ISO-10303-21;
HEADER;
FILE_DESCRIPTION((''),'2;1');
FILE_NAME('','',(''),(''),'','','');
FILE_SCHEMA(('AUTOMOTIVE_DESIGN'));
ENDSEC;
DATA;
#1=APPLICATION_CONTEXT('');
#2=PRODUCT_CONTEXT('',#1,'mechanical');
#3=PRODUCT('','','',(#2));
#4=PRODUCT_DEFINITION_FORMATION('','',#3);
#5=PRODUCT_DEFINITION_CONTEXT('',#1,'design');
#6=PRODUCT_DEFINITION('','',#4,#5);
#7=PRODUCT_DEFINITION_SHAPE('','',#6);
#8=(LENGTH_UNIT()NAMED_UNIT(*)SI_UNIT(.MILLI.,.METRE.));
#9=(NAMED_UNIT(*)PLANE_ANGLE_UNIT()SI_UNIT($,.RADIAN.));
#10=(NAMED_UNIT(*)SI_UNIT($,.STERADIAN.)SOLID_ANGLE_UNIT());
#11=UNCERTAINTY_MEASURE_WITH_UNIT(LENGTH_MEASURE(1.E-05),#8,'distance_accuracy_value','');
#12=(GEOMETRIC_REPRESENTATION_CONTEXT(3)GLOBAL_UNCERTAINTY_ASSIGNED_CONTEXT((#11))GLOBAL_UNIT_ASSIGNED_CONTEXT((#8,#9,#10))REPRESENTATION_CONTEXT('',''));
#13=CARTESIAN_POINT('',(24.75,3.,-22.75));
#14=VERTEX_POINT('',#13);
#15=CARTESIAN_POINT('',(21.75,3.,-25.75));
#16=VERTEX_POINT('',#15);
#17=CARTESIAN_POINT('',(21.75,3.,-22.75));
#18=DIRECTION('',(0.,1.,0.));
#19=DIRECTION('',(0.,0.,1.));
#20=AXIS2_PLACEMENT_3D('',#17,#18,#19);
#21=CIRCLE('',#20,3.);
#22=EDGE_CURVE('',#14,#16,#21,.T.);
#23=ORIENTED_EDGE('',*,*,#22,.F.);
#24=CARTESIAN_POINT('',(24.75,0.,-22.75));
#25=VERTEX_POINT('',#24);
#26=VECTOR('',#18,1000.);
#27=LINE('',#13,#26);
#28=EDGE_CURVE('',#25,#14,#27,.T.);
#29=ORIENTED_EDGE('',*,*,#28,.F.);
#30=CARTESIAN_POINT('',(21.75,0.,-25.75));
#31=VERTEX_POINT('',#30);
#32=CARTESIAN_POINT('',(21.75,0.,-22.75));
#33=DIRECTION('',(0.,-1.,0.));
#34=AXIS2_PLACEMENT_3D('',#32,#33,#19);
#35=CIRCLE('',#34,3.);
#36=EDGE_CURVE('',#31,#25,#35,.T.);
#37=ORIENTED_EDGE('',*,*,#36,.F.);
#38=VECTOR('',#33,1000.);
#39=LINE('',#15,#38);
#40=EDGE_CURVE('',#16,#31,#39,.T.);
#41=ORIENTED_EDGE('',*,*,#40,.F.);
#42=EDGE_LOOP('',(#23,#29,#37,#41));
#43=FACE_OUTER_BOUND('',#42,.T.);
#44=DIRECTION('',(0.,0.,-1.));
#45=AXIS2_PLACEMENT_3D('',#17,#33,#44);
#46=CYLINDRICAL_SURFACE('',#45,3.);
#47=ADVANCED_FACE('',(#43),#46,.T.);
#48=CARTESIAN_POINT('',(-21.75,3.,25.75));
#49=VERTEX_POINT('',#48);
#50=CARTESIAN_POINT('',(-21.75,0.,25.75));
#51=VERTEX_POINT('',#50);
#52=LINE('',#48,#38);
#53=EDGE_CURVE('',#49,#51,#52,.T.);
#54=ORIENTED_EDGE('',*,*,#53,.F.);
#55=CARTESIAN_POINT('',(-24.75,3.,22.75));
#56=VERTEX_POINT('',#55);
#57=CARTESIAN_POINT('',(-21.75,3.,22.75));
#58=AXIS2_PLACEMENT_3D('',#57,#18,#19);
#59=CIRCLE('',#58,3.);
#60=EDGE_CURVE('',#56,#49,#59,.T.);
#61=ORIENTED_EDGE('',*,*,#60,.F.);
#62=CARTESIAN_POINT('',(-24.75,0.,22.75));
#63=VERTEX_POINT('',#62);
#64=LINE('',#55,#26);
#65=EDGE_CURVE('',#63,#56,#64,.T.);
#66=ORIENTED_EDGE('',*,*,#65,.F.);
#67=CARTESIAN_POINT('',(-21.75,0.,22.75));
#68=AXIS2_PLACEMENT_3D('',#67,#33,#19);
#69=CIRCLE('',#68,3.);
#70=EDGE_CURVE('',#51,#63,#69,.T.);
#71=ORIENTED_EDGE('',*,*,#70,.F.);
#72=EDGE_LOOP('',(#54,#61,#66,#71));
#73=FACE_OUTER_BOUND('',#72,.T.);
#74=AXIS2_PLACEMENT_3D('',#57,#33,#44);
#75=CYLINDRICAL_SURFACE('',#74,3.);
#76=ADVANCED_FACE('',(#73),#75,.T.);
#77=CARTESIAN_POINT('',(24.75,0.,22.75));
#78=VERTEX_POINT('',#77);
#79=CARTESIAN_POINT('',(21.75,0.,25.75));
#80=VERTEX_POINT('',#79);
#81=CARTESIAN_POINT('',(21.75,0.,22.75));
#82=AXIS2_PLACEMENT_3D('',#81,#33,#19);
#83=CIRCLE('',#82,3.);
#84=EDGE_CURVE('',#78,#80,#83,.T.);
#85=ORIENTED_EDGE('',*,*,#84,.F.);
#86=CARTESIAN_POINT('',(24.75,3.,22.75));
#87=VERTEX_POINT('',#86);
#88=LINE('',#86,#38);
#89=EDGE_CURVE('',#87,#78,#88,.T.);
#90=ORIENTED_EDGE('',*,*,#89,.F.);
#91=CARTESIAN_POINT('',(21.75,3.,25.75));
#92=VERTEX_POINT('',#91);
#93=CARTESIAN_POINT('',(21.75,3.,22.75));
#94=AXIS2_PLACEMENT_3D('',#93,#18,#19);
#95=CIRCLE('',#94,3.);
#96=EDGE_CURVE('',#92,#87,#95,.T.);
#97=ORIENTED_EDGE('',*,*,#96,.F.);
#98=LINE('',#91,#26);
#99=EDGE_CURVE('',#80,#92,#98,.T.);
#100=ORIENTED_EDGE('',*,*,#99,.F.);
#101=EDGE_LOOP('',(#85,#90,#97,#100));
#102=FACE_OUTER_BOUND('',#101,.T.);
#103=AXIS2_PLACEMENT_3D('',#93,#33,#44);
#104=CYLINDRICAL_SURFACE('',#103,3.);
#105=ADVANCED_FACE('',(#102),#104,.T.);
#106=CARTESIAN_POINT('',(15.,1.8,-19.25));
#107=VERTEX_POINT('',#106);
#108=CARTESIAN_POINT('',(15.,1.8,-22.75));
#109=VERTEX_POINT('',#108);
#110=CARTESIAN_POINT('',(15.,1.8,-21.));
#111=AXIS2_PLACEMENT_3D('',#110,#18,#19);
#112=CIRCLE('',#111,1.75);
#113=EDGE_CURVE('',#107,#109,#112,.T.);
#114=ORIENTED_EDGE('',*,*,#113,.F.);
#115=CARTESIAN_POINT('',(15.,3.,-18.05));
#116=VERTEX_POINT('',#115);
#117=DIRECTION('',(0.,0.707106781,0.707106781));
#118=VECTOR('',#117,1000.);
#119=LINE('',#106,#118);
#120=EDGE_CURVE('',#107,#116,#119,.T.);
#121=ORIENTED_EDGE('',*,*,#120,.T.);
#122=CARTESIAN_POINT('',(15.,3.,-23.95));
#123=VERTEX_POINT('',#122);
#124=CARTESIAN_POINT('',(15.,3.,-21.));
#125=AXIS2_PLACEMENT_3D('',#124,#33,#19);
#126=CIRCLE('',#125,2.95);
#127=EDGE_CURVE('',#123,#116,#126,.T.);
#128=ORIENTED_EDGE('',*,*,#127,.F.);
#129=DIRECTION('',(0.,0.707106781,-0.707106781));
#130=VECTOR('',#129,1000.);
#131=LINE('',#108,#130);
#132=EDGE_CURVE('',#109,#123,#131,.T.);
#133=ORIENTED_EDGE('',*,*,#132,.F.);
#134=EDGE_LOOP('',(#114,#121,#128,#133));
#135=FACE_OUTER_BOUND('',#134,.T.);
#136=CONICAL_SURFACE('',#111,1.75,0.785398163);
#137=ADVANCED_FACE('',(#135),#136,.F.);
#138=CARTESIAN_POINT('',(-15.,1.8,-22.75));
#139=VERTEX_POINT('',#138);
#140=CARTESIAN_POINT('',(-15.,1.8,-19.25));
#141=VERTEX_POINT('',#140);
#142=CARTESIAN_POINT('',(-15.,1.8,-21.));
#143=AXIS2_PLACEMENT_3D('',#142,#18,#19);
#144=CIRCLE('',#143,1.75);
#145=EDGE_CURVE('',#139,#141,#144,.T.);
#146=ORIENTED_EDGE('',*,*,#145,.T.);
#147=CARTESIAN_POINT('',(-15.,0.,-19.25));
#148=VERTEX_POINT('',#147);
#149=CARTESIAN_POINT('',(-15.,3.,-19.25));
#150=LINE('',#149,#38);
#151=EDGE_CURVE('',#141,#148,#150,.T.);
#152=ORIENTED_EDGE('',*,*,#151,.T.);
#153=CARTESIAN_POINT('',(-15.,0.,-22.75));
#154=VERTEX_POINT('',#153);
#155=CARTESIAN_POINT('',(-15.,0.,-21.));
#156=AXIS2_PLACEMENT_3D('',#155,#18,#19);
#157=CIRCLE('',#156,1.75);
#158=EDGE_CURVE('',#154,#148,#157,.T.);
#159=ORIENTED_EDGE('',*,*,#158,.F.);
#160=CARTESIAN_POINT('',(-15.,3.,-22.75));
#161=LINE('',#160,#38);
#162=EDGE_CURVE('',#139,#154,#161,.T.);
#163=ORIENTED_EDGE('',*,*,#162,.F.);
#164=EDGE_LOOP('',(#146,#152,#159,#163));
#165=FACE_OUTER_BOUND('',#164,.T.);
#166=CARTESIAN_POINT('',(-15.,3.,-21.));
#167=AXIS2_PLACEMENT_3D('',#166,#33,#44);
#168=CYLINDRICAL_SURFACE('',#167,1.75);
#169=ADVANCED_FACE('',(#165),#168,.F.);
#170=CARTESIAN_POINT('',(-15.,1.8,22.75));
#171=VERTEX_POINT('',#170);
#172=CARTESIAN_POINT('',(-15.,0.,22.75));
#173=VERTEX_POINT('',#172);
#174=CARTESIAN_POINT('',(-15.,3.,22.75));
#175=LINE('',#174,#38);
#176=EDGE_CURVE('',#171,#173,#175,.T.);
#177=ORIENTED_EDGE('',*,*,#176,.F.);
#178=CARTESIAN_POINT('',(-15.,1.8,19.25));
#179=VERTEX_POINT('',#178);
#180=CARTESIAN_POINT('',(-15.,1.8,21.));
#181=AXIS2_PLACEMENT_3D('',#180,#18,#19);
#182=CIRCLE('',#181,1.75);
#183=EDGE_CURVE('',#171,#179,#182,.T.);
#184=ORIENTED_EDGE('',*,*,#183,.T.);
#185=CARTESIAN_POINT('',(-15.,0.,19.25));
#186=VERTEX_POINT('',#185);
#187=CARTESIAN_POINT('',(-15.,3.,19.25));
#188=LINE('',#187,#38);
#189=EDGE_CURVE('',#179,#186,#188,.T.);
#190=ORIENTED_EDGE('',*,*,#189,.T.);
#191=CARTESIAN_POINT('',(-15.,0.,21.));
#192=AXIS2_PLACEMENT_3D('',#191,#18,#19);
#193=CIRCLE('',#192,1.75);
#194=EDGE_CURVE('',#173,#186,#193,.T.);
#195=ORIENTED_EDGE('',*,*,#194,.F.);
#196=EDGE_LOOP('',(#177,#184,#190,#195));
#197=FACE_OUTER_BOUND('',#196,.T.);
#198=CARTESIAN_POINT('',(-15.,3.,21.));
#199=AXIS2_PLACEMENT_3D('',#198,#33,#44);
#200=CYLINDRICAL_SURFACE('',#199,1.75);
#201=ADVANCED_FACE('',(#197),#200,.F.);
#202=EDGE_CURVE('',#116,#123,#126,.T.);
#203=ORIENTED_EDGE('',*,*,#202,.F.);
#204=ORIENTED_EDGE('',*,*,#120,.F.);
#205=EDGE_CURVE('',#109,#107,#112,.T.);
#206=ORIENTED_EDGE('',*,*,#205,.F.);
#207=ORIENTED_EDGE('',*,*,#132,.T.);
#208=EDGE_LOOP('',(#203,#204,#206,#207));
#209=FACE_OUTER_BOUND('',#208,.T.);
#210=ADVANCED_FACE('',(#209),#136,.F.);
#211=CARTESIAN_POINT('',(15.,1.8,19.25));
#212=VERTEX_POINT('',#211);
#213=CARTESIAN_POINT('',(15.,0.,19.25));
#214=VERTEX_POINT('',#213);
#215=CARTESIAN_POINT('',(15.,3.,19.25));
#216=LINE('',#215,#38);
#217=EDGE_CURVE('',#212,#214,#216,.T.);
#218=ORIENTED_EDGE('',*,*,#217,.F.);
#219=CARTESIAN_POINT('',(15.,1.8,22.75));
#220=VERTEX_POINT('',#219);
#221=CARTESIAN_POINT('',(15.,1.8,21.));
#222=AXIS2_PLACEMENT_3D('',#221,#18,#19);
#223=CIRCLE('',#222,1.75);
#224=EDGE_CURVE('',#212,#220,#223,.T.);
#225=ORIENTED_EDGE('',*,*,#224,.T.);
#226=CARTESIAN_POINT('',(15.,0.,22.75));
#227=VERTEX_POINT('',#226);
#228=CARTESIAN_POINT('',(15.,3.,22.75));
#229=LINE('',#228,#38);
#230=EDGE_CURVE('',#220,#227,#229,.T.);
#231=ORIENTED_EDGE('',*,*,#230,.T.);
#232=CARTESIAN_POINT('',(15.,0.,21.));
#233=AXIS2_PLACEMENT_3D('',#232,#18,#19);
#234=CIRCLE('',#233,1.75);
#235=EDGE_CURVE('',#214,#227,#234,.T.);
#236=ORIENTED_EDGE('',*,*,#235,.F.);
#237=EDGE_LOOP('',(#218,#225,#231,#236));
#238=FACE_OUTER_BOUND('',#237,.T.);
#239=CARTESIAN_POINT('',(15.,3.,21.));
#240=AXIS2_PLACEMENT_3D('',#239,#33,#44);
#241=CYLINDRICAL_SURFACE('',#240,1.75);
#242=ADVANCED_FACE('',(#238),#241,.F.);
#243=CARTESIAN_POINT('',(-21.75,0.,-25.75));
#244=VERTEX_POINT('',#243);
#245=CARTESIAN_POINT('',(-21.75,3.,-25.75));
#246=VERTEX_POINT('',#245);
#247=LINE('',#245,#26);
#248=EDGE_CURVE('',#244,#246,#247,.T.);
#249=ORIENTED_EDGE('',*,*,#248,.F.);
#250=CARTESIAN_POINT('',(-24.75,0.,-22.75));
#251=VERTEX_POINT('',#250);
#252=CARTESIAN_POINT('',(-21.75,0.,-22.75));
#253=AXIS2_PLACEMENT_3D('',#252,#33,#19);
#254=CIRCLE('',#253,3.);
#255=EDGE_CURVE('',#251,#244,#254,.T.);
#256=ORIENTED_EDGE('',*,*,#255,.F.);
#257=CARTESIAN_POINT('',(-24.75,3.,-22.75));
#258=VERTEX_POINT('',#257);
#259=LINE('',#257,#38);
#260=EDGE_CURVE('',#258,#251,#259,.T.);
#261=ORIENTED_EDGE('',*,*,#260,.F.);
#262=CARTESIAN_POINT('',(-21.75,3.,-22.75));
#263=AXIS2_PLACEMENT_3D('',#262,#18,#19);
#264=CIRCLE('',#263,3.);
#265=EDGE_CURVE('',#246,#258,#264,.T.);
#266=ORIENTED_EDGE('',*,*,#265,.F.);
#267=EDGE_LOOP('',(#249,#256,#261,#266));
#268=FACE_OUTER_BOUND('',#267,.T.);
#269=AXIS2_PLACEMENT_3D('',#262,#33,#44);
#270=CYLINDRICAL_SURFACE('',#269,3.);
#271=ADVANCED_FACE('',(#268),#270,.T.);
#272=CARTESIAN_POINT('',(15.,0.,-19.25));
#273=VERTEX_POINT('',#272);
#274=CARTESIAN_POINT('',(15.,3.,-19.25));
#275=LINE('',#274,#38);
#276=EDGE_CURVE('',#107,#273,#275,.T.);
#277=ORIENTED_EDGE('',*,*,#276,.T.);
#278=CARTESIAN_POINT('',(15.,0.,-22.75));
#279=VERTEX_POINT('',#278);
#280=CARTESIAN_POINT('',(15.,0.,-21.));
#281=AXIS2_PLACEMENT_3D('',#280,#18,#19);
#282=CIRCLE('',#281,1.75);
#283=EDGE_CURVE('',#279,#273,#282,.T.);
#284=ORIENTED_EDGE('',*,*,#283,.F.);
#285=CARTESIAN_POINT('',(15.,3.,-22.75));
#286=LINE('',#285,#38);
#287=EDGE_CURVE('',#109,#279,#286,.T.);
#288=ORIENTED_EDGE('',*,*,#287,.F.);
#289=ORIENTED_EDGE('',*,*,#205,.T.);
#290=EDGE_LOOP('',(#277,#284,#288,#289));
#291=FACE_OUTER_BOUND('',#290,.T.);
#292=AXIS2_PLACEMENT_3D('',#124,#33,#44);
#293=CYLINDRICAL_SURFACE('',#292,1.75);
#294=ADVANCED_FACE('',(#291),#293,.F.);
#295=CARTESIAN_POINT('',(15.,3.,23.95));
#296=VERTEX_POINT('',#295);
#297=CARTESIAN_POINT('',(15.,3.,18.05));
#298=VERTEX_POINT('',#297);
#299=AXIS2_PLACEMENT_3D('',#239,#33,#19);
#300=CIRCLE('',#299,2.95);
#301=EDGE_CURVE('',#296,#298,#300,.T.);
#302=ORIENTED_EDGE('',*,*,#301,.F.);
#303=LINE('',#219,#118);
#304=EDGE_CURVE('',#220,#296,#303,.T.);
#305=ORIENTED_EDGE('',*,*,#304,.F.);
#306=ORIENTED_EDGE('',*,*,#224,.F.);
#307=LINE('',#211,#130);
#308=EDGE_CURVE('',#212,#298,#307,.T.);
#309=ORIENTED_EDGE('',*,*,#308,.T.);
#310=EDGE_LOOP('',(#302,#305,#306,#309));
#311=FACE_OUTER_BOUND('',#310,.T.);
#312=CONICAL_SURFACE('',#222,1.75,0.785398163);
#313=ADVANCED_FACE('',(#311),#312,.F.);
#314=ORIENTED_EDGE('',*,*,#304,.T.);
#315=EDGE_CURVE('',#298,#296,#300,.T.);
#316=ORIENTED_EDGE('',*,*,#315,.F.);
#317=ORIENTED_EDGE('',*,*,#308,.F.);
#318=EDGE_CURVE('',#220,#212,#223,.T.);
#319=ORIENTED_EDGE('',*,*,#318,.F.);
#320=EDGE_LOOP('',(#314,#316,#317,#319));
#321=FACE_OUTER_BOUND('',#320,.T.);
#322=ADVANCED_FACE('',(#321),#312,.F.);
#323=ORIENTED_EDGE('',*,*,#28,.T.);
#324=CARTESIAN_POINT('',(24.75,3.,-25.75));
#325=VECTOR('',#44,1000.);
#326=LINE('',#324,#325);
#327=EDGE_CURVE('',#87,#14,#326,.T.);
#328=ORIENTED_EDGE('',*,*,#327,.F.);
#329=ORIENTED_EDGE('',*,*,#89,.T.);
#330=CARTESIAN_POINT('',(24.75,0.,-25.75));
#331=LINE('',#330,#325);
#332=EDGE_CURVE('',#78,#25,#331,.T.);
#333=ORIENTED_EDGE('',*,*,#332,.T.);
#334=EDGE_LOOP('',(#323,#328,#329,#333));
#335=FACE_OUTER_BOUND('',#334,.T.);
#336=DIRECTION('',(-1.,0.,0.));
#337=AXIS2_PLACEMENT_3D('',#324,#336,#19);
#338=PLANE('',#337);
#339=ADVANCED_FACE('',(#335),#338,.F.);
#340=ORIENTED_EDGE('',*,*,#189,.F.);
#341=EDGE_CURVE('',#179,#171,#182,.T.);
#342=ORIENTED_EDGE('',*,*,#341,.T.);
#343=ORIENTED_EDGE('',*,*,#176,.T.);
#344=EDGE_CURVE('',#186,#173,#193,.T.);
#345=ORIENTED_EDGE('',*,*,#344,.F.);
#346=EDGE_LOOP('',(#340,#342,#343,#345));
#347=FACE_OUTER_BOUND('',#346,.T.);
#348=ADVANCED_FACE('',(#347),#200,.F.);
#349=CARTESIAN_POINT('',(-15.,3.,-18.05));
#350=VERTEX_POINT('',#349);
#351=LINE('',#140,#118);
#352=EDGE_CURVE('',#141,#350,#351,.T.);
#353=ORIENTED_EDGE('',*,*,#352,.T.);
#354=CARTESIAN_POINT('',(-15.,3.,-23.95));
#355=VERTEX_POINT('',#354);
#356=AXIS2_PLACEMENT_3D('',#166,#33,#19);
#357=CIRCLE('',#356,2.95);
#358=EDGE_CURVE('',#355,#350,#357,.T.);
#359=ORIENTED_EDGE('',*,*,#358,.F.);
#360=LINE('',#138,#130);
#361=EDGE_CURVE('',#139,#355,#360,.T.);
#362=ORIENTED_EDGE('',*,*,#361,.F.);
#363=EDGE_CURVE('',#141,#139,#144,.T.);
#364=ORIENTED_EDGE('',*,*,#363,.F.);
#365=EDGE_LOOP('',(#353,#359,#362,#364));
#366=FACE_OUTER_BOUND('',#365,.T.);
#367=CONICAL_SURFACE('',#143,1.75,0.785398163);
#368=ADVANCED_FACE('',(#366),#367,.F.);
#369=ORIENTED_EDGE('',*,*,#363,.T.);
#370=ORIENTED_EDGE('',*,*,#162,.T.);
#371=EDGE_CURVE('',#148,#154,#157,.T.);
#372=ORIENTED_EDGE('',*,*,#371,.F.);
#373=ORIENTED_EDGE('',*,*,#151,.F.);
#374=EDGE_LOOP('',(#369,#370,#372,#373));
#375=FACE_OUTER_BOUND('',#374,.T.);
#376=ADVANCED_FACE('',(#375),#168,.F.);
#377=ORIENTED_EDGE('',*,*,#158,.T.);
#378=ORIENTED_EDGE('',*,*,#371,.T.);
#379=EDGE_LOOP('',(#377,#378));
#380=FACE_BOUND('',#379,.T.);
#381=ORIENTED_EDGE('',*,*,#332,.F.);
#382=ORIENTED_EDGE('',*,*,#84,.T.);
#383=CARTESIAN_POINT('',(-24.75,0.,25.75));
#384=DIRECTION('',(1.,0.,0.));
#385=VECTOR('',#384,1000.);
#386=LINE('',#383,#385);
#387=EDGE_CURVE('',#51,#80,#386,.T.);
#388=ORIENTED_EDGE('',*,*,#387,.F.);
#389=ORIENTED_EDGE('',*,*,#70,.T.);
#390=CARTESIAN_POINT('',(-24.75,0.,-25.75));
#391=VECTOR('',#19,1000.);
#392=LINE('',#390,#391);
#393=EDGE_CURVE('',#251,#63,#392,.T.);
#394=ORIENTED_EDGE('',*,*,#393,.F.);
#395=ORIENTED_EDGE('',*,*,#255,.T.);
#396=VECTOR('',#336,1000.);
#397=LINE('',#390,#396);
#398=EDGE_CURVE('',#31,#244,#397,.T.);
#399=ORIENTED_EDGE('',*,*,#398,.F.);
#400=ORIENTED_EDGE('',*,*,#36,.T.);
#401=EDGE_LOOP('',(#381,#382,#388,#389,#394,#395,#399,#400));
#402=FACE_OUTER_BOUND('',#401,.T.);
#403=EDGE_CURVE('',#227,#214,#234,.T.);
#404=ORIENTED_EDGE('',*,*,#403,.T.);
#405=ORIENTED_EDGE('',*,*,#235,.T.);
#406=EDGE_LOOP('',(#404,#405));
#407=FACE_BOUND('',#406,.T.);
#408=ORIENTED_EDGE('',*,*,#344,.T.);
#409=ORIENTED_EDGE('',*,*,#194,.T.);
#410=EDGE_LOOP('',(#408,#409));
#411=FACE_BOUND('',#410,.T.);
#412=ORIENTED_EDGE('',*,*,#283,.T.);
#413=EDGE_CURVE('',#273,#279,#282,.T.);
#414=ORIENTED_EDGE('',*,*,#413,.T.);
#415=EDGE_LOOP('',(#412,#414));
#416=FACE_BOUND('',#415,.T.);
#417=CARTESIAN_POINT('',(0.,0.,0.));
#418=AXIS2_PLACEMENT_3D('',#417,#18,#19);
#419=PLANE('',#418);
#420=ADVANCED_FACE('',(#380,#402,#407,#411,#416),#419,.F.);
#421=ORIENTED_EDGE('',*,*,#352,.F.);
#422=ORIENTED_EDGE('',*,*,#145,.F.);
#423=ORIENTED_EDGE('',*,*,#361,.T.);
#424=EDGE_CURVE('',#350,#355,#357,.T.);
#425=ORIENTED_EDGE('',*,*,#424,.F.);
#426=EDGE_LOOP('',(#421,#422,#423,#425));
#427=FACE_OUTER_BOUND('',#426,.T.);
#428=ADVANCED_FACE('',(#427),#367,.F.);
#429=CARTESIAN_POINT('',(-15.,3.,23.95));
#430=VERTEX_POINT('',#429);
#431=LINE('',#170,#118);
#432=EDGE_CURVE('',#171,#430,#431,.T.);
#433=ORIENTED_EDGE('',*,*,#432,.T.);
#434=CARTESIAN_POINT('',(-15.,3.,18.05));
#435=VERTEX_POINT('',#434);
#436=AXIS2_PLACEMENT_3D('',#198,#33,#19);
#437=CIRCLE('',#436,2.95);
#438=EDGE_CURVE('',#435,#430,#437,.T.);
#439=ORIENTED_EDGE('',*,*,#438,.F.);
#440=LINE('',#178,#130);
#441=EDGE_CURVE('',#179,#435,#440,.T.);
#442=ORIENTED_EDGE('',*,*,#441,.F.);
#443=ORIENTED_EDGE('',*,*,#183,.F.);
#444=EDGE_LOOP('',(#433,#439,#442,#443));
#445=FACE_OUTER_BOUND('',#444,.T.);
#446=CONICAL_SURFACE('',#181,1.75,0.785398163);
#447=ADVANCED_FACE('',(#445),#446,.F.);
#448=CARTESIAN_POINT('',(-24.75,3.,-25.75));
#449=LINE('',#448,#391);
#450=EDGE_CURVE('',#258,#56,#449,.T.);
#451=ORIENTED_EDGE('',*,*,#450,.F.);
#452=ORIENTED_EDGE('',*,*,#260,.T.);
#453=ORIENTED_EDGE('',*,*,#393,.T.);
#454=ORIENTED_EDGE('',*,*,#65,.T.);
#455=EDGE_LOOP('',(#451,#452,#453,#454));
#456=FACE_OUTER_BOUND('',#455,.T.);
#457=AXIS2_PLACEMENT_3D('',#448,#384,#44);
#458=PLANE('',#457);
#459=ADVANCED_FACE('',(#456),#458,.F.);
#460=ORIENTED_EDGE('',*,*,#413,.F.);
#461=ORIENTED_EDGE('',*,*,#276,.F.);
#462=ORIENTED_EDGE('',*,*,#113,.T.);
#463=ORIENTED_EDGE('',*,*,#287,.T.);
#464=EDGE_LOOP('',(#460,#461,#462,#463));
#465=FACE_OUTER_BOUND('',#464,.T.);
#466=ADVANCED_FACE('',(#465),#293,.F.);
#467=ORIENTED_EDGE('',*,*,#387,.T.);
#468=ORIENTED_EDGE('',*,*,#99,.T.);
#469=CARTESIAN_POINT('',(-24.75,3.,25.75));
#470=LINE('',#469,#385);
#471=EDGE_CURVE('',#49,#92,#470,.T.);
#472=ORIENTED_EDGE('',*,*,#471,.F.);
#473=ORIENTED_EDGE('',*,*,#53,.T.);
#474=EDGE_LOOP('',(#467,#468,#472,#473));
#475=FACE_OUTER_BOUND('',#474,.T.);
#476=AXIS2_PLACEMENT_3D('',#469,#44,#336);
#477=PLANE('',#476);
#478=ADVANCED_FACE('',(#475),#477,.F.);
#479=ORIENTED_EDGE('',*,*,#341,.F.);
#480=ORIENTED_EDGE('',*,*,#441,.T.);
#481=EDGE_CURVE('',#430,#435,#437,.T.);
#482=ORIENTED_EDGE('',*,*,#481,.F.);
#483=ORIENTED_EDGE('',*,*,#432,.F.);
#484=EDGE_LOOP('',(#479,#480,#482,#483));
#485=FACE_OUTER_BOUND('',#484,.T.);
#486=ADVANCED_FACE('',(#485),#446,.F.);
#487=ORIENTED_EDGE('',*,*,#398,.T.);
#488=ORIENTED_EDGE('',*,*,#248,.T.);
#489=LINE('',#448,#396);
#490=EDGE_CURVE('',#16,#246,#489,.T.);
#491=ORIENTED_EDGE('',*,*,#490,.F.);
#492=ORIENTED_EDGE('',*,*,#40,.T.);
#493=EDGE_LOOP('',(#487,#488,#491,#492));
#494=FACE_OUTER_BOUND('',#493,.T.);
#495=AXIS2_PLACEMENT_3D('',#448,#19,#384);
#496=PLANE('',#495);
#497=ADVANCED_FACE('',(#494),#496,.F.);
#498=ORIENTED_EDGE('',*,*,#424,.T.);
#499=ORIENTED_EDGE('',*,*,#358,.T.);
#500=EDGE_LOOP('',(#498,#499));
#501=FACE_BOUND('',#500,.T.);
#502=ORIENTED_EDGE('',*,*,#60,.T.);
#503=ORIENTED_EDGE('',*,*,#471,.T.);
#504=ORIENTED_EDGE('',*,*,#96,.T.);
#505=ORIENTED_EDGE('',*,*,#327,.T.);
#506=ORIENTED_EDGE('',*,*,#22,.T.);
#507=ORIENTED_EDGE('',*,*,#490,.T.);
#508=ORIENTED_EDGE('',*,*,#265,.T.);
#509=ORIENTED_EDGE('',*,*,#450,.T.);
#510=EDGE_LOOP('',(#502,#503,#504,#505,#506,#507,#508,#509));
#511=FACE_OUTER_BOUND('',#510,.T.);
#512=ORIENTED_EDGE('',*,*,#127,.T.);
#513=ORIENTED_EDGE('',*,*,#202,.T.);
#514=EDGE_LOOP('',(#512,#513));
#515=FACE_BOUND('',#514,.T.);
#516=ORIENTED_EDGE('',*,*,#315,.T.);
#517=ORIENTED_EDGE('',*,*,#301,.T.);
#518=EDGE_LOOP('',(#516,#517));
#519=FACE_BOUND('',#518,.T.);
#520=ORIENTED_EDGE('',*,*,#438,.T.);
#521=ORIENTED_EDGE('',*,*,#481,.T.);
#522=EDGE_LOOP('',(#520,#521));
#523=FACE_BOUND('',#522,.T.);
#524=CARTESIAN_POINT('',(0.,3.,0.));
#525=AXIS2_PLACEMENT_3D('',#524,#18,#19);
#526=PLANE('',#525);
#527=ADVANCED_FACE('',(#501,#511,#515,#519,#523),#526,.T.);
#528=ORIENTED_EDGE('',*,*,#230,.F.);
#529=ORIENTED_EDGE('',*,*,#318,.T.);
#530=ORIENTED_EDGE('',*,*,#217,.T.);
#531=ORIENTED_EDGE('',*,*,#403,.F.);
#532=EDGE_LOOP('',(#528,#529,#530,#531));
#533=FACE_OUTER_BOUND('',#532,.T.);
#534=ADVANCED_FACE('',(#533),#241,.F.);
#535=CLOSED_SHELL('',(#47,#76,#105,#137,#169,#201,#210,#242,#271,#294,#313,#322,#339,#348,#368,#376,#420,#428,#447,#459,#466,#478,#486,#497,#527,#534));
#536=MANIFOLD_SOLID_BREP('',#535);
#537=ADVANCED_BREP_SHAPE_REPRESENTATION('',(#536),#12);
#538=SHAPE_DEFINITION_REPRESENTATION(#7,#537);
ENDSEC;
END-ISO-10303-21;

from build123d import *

# Parameters (mm, degrees)
SKETCH1_W           = 49.5
SKETCH1_H           = 51.5
SKETCH1_R           = 1.75
BOSS_EXTRUDE1_DEPTH = 3
CHAMFER1_SIZE       = 1.2
FILLET1_R           = 3


with BuildPart() as part:
    # Sketch1 → Boss-Extrude1 (new body)
    with BuildSketch(Plane(origin=(0, 0, 0), x_dir=(1, 0, 0), z_dir=(0, 1, 0))):
        Rectangle(SKETCH1_W, SKETCH1_H)
        with Locations(Location((-15, 21, 0), (0, 0, 270))):
            Circle(SKETCH1_R, mode=Mode.SUBTRACT)
        with Locations(Location((15, 21, 0), (0, 0, 270))):
            Circle(SKETCH1_R, mode=Mode.SUBTRACT)
        with Locations(Location((-15, -21, 0), (0, 0, 270))):
            Circle(SKETCH1_R, mode=Mode.SUBTRACT)
        with Locations(Location((15, -21, 0), (0, 0, 270))):
            Circle(SKETCH1_R, mode=Mode.SUBTRACT)
    extrude(amount=BOSS_EXTRUDE1_DEPTH)

    # Chamfer1
    chamfer1_edges = [part.edges().sort_by_distance(p)[0] for p in [
        (-15, 3, -22.75),
        (15, 3, -22.75),
        (-15, 3, 19.25),
        (15, 3, 19.25),
    ]]
    chamfer(chamfer1_edges, length=CHAMFER1_SIZE)

    # Fillet1
    fillet1_edges = [part.edges().sort_by_distance(p)[0] for p in [
        (24.75, 1.5, 25.75),
        (-24.75, 1.5, 25.75),
        (-24.75, 1.5, -25.75),
        (24.75, 1.5, -25.75),
    ]]
    fillet(fillet1_edges, radius=FILLET1_R)


solid = part.part
